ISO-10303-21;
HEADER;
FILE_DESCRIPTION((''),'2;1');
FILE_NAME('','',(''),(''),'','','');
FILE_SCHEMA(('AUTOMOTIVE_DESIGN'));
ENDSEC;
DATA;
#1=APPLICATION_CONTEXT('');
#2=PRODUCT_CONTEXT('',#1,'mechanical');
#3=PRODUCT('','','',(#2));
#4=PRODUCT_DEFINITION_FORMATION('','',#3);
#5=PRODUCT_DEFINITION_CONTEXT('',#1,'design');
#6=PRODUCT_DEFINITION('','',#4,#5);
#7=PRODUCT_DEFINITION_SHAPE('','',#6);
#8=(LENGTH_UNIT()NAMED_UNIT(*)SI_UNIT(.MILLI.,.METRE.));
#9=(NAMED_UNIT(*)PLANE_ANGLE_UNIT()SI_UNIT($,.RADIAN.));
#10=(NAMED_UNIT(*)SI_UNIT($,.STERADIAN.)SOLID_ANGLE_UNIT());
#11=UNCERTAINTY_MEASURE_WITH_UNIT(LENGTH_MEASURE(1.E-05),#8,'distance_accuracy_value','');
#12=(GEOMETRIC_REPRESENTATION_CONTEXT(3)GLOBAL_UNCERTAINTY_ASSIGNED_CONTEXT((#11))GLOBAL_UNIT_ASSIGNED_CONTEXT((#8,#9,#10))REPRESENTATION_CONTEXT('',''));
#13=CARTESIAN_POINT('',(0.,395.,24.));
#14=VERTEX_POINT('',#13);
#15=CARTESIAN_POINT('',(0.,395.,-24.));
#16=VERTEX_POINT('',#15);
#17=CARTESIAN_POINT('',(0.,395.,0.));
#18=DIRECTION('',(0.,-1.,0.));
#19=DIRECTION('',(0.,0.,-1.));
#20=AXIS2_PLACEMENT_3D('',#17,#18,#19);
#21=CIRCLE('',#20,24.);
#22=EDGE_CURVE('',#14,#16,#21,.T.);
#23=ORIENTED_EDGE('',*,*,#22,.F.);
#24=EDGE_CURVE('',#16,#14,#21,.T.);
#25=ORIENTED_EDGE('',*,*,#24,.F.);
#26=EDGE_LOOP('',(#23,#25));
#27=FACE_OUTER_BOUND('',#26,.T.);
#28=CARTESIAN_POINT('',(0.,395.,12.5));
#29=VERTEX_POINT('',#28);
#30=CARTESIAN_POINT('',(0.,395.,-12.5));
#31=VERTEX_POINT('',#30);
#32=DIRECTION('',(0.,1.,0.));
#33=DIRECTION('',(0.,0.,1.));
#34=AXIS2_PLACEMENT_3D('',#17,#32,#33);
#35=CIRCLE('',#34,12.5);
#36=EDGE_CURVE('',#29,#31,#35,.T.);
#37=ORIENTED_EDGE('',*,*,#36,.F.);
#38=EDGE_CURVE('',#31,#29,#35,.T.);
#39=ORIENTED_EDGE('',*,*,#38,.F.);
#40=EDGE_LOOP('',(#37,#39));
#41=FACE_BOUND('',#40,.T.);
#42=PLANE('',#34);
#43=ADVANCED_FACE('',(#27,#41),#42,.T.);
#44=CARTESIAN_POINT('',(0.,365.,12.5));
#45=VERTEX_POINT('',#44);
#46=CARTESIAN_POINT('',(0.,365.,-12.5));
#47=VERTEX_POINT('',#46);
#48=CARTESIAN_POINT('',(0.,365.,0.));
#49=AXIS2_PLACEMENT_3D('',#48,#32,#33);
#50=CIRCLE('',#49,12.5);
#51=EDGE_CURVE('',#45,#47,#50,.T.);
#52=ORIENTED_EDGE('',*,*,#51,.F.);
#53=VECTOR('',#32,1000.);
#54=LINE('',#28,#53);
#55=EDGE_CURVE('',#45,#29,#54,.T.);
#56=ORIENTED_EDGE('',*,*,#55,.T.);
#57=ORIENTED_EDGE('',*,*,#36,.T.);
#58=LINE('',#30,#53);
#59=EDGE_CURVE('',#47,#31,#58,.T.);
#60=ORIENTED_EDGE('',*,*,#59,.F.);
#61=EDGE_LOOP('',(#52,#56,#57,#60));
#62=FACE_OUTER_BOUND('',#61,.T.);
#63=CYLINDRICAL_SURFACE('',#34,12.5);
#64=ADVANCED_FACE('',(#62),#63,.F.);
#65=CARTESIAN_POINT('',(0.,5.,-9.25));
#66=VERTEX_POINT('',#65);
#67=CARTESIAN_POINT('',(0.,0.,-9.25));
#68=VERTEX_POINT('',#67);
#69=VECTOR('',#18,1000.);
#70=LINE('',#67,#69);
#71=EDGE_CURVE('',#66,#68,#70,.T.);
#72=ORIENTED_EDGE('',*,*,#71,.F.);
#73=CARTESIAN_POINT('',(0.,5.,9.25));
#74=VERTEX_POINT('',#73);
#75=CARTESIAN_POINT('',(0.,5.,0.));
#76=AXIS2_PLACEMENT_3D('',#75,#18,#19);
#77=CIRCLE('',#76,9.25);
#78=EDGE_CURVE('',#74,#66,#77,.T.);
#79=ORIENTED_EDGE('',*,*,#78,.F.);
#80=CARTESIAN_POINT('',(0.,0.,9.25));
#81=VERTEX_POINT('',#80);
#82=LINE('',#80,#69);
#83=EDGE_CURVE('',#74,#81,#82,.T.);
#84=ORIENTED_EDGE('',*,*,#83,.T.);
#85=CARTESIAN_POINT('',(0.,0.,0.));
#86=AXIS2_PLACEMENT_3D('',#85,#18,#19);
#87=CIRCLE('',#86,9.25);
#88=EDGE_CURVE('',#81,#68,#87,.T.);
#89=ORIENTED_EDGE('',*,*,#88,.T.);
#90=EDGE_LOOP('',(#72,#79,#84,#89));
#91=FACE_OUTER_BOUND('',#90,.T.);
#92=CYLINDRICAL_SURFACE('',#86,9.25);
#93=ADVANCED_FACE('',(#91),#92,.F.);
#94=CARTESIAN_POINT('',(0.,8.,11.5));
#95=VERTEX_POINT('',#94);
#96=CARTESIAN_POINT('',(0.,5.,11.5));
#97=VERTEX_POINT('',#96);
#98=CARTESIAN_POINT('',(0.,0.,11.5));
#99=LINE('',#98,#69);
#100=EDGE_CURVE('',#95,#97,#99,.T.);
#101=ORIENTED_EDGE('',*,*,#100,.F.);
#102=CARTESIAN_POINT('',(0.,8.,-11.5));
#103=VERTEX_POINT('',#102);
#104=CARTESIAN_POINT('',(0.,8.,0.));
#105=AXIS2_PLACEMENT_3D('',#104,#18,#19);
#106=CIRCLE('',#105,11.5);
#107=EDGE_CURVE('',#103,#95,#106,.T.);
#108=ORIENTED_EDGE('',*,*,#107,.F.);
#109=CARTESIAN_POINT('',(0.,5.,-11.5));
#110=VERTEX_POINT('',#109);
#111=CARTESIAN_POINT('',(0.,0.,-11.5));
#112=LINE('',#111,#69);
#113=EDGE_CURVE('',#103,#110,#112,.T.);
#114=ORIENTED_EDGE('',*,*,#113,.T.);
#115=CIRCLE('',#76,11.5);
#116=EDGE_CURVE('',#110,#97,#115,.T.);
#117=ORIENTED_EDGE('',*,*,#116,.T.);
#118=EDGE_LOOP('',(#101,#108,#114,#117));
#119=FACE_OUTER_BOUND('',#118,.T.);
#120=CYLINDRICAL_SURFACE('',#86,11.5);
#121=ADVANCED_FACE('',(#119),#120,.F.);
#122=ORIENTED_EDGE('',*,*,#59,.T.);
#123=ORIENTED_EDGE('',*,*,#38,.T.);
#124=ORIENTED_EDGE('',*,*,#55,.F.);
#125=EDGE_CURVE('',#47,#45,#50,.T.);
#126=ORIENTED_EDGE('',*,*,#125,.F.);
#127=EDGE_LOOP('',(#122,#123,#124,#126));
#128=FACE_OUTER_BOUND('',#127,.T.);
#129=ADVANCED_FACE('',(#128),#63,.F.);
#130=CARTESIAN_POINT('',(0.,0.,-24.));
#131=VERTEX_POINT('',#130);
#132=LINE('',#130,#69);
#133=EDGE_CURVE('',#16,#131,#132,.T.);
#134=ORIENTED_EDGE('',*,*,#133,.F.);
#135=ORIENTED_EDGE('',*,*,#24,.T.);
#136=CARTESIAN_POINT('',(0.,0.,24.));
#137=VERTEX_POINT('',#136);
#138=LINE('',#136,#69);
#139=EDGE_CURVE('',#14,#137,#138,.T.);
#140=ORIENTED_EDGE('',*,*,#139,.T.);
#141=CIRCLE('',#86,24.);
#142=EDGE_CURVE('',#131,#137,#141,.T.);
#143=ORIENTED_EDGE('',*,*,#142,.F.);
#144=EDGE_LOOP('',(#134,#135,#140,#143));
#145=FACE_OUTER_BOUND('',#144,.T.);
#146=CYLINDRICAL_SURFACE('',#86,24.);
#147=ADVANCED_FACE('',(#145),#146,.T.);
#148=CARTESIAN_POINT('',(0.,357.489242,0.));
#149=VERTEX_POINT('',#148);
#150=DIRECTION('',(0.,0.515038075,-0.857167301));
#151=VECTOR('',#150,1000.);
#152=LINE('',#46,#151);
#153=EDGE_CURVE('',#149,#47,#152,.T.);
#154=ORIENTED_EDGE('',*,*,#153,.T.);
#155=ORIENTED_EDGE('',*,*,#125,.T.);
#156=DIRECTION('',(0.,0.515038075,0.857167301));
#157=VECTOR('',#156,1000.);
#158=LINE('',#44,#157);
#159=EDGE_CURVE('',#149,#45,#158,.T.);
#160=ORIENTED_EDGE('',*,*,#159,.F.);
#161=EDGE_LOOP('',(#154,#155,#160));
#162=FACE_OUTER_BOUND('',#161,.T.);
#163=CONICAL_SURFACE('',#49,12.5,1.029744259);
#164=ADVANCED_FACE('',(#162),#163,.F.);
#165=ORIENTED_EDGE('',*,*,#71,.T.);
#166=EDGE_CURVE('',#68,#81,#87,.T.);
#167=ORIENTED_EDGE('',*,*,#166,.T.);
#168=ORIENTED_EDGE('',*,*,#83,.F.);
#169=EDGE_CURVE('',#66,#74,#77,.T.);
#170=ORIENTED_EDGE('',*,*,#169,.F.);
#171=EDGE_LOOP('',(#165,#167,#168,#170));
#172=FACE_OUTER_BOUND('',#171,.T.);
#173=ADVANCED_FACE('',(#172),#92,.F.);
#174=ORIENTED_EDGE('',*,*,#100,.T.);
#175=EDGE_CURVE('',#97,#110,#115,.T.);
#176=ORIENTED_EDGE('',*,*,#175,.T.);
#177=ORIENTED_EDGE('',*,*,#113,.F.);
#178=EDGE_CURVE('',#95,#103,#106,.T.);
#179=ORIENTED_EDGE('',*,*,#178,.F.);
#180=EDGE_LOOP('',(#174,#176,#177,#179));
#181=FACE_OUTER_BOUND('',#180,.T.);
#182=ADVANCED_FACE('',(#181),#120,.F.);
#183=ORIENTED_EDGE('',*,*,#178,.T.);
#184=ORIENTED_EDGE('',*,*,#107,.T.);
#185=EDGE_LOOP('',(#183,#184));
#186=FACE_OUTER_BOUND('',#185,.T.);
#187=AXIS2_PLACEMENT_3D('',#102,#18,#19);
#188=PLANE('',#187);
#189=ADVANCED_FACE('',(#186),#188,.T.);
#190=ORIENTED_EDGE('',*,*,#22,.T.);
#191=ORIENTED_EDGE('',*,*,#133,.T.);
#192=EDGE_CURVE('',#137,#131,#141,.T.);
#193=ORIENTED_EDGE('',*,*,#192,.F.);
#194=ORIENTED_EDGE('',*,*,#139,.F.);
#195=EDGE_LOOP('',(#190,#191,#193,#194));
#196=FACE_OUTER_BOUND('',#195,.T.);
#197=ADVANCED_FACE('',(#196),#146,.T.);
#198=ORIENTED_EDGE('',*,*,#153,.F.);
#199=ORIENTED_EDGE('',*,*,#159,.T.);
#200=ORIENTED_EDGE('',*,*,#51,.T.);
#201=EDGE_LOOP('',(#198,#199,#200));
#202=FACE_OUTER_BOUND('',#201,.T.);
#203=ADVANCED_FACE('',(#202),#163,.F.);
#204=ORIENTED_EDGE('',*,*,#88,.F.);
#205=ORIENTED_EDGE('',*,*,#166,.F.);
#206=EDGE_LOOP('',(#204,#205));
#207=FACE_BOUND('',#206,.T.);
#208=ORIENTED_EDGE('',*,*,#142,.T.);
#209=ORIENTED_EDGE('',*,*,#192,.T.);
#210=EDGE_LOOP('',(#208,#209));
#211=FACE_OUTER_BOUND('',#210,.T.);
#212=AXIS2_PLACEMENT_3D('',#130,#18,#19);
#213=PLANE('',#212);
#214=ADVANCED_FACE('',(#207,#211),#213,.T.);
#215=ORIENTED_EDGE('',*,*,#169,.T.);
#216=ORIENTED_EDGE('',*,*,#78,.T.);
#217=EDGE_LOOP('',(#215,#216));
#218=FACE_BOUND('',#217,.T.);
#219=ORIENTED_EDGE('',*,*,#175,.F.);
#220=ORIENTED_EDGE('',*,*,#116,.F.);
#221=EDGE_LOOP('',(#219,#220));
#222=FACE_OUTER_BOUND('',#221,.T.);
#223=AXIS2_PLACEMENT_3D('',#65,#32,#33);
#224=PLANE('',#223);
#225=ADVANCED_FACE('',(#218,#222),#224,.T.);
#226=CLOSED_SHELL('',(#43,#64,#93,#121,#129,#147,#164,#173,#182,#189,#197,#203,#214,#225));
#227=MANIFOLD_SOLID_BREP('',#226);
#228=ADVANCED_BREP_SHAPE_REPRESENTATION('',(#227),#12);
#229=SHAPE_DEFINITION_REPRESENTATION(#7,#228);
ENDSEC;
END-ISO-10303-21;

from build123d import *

# Parameters (mm, degrees)
F_25_0_25_DIAMETER_HOLE1_D     = 25
F_25_0_25_DIAMETER_HOLE1_DEPTH = 30
F_25_0_25_DIAMETER_HOLE1_TIP   = 7.510757738


with BuildPart() as part:
    # Sketch1 → Revolve1 (revolve)
    with BuildSketch(Plane(origin=(0, 0, 0), x_dir=(0, 0, -1), z_dir=(1, 0, 0))):
        Polygon((0, 395), (24, 395), (24, 0), (9.25, 0), (9.25, 5), (11.5, 5), (11.5, 8), (0, 8), align=None)
    revolve(axis=Axis((0, 0, 0), (0, 1, 0)))

    # Ø25.0 (25) Diameter Hole1
    with Locations(Plane.ZX.offset(395)):
        with Locations((0, 0)):
            Hole(F_25_0_25_DIAMETER_HOLE1_D / 2, depth=F_25_0_25_DIAMETER_HOLE1_DEPTH)
            with Locations((0, 0, -(F_25_0_25_DIAMETER_HOLE1_DEPTH + F_25_0_25_DIAMETER_HOLE1_TIP / 2))):  # 118° drill point
                Cone(0, F_25_0_25_DIAMETER_HOLE1_D / 2, F_25_0_25_DIAMETER_HOLE1_TIP, mode=Mode.SUBTRACT)


solid = part.part
